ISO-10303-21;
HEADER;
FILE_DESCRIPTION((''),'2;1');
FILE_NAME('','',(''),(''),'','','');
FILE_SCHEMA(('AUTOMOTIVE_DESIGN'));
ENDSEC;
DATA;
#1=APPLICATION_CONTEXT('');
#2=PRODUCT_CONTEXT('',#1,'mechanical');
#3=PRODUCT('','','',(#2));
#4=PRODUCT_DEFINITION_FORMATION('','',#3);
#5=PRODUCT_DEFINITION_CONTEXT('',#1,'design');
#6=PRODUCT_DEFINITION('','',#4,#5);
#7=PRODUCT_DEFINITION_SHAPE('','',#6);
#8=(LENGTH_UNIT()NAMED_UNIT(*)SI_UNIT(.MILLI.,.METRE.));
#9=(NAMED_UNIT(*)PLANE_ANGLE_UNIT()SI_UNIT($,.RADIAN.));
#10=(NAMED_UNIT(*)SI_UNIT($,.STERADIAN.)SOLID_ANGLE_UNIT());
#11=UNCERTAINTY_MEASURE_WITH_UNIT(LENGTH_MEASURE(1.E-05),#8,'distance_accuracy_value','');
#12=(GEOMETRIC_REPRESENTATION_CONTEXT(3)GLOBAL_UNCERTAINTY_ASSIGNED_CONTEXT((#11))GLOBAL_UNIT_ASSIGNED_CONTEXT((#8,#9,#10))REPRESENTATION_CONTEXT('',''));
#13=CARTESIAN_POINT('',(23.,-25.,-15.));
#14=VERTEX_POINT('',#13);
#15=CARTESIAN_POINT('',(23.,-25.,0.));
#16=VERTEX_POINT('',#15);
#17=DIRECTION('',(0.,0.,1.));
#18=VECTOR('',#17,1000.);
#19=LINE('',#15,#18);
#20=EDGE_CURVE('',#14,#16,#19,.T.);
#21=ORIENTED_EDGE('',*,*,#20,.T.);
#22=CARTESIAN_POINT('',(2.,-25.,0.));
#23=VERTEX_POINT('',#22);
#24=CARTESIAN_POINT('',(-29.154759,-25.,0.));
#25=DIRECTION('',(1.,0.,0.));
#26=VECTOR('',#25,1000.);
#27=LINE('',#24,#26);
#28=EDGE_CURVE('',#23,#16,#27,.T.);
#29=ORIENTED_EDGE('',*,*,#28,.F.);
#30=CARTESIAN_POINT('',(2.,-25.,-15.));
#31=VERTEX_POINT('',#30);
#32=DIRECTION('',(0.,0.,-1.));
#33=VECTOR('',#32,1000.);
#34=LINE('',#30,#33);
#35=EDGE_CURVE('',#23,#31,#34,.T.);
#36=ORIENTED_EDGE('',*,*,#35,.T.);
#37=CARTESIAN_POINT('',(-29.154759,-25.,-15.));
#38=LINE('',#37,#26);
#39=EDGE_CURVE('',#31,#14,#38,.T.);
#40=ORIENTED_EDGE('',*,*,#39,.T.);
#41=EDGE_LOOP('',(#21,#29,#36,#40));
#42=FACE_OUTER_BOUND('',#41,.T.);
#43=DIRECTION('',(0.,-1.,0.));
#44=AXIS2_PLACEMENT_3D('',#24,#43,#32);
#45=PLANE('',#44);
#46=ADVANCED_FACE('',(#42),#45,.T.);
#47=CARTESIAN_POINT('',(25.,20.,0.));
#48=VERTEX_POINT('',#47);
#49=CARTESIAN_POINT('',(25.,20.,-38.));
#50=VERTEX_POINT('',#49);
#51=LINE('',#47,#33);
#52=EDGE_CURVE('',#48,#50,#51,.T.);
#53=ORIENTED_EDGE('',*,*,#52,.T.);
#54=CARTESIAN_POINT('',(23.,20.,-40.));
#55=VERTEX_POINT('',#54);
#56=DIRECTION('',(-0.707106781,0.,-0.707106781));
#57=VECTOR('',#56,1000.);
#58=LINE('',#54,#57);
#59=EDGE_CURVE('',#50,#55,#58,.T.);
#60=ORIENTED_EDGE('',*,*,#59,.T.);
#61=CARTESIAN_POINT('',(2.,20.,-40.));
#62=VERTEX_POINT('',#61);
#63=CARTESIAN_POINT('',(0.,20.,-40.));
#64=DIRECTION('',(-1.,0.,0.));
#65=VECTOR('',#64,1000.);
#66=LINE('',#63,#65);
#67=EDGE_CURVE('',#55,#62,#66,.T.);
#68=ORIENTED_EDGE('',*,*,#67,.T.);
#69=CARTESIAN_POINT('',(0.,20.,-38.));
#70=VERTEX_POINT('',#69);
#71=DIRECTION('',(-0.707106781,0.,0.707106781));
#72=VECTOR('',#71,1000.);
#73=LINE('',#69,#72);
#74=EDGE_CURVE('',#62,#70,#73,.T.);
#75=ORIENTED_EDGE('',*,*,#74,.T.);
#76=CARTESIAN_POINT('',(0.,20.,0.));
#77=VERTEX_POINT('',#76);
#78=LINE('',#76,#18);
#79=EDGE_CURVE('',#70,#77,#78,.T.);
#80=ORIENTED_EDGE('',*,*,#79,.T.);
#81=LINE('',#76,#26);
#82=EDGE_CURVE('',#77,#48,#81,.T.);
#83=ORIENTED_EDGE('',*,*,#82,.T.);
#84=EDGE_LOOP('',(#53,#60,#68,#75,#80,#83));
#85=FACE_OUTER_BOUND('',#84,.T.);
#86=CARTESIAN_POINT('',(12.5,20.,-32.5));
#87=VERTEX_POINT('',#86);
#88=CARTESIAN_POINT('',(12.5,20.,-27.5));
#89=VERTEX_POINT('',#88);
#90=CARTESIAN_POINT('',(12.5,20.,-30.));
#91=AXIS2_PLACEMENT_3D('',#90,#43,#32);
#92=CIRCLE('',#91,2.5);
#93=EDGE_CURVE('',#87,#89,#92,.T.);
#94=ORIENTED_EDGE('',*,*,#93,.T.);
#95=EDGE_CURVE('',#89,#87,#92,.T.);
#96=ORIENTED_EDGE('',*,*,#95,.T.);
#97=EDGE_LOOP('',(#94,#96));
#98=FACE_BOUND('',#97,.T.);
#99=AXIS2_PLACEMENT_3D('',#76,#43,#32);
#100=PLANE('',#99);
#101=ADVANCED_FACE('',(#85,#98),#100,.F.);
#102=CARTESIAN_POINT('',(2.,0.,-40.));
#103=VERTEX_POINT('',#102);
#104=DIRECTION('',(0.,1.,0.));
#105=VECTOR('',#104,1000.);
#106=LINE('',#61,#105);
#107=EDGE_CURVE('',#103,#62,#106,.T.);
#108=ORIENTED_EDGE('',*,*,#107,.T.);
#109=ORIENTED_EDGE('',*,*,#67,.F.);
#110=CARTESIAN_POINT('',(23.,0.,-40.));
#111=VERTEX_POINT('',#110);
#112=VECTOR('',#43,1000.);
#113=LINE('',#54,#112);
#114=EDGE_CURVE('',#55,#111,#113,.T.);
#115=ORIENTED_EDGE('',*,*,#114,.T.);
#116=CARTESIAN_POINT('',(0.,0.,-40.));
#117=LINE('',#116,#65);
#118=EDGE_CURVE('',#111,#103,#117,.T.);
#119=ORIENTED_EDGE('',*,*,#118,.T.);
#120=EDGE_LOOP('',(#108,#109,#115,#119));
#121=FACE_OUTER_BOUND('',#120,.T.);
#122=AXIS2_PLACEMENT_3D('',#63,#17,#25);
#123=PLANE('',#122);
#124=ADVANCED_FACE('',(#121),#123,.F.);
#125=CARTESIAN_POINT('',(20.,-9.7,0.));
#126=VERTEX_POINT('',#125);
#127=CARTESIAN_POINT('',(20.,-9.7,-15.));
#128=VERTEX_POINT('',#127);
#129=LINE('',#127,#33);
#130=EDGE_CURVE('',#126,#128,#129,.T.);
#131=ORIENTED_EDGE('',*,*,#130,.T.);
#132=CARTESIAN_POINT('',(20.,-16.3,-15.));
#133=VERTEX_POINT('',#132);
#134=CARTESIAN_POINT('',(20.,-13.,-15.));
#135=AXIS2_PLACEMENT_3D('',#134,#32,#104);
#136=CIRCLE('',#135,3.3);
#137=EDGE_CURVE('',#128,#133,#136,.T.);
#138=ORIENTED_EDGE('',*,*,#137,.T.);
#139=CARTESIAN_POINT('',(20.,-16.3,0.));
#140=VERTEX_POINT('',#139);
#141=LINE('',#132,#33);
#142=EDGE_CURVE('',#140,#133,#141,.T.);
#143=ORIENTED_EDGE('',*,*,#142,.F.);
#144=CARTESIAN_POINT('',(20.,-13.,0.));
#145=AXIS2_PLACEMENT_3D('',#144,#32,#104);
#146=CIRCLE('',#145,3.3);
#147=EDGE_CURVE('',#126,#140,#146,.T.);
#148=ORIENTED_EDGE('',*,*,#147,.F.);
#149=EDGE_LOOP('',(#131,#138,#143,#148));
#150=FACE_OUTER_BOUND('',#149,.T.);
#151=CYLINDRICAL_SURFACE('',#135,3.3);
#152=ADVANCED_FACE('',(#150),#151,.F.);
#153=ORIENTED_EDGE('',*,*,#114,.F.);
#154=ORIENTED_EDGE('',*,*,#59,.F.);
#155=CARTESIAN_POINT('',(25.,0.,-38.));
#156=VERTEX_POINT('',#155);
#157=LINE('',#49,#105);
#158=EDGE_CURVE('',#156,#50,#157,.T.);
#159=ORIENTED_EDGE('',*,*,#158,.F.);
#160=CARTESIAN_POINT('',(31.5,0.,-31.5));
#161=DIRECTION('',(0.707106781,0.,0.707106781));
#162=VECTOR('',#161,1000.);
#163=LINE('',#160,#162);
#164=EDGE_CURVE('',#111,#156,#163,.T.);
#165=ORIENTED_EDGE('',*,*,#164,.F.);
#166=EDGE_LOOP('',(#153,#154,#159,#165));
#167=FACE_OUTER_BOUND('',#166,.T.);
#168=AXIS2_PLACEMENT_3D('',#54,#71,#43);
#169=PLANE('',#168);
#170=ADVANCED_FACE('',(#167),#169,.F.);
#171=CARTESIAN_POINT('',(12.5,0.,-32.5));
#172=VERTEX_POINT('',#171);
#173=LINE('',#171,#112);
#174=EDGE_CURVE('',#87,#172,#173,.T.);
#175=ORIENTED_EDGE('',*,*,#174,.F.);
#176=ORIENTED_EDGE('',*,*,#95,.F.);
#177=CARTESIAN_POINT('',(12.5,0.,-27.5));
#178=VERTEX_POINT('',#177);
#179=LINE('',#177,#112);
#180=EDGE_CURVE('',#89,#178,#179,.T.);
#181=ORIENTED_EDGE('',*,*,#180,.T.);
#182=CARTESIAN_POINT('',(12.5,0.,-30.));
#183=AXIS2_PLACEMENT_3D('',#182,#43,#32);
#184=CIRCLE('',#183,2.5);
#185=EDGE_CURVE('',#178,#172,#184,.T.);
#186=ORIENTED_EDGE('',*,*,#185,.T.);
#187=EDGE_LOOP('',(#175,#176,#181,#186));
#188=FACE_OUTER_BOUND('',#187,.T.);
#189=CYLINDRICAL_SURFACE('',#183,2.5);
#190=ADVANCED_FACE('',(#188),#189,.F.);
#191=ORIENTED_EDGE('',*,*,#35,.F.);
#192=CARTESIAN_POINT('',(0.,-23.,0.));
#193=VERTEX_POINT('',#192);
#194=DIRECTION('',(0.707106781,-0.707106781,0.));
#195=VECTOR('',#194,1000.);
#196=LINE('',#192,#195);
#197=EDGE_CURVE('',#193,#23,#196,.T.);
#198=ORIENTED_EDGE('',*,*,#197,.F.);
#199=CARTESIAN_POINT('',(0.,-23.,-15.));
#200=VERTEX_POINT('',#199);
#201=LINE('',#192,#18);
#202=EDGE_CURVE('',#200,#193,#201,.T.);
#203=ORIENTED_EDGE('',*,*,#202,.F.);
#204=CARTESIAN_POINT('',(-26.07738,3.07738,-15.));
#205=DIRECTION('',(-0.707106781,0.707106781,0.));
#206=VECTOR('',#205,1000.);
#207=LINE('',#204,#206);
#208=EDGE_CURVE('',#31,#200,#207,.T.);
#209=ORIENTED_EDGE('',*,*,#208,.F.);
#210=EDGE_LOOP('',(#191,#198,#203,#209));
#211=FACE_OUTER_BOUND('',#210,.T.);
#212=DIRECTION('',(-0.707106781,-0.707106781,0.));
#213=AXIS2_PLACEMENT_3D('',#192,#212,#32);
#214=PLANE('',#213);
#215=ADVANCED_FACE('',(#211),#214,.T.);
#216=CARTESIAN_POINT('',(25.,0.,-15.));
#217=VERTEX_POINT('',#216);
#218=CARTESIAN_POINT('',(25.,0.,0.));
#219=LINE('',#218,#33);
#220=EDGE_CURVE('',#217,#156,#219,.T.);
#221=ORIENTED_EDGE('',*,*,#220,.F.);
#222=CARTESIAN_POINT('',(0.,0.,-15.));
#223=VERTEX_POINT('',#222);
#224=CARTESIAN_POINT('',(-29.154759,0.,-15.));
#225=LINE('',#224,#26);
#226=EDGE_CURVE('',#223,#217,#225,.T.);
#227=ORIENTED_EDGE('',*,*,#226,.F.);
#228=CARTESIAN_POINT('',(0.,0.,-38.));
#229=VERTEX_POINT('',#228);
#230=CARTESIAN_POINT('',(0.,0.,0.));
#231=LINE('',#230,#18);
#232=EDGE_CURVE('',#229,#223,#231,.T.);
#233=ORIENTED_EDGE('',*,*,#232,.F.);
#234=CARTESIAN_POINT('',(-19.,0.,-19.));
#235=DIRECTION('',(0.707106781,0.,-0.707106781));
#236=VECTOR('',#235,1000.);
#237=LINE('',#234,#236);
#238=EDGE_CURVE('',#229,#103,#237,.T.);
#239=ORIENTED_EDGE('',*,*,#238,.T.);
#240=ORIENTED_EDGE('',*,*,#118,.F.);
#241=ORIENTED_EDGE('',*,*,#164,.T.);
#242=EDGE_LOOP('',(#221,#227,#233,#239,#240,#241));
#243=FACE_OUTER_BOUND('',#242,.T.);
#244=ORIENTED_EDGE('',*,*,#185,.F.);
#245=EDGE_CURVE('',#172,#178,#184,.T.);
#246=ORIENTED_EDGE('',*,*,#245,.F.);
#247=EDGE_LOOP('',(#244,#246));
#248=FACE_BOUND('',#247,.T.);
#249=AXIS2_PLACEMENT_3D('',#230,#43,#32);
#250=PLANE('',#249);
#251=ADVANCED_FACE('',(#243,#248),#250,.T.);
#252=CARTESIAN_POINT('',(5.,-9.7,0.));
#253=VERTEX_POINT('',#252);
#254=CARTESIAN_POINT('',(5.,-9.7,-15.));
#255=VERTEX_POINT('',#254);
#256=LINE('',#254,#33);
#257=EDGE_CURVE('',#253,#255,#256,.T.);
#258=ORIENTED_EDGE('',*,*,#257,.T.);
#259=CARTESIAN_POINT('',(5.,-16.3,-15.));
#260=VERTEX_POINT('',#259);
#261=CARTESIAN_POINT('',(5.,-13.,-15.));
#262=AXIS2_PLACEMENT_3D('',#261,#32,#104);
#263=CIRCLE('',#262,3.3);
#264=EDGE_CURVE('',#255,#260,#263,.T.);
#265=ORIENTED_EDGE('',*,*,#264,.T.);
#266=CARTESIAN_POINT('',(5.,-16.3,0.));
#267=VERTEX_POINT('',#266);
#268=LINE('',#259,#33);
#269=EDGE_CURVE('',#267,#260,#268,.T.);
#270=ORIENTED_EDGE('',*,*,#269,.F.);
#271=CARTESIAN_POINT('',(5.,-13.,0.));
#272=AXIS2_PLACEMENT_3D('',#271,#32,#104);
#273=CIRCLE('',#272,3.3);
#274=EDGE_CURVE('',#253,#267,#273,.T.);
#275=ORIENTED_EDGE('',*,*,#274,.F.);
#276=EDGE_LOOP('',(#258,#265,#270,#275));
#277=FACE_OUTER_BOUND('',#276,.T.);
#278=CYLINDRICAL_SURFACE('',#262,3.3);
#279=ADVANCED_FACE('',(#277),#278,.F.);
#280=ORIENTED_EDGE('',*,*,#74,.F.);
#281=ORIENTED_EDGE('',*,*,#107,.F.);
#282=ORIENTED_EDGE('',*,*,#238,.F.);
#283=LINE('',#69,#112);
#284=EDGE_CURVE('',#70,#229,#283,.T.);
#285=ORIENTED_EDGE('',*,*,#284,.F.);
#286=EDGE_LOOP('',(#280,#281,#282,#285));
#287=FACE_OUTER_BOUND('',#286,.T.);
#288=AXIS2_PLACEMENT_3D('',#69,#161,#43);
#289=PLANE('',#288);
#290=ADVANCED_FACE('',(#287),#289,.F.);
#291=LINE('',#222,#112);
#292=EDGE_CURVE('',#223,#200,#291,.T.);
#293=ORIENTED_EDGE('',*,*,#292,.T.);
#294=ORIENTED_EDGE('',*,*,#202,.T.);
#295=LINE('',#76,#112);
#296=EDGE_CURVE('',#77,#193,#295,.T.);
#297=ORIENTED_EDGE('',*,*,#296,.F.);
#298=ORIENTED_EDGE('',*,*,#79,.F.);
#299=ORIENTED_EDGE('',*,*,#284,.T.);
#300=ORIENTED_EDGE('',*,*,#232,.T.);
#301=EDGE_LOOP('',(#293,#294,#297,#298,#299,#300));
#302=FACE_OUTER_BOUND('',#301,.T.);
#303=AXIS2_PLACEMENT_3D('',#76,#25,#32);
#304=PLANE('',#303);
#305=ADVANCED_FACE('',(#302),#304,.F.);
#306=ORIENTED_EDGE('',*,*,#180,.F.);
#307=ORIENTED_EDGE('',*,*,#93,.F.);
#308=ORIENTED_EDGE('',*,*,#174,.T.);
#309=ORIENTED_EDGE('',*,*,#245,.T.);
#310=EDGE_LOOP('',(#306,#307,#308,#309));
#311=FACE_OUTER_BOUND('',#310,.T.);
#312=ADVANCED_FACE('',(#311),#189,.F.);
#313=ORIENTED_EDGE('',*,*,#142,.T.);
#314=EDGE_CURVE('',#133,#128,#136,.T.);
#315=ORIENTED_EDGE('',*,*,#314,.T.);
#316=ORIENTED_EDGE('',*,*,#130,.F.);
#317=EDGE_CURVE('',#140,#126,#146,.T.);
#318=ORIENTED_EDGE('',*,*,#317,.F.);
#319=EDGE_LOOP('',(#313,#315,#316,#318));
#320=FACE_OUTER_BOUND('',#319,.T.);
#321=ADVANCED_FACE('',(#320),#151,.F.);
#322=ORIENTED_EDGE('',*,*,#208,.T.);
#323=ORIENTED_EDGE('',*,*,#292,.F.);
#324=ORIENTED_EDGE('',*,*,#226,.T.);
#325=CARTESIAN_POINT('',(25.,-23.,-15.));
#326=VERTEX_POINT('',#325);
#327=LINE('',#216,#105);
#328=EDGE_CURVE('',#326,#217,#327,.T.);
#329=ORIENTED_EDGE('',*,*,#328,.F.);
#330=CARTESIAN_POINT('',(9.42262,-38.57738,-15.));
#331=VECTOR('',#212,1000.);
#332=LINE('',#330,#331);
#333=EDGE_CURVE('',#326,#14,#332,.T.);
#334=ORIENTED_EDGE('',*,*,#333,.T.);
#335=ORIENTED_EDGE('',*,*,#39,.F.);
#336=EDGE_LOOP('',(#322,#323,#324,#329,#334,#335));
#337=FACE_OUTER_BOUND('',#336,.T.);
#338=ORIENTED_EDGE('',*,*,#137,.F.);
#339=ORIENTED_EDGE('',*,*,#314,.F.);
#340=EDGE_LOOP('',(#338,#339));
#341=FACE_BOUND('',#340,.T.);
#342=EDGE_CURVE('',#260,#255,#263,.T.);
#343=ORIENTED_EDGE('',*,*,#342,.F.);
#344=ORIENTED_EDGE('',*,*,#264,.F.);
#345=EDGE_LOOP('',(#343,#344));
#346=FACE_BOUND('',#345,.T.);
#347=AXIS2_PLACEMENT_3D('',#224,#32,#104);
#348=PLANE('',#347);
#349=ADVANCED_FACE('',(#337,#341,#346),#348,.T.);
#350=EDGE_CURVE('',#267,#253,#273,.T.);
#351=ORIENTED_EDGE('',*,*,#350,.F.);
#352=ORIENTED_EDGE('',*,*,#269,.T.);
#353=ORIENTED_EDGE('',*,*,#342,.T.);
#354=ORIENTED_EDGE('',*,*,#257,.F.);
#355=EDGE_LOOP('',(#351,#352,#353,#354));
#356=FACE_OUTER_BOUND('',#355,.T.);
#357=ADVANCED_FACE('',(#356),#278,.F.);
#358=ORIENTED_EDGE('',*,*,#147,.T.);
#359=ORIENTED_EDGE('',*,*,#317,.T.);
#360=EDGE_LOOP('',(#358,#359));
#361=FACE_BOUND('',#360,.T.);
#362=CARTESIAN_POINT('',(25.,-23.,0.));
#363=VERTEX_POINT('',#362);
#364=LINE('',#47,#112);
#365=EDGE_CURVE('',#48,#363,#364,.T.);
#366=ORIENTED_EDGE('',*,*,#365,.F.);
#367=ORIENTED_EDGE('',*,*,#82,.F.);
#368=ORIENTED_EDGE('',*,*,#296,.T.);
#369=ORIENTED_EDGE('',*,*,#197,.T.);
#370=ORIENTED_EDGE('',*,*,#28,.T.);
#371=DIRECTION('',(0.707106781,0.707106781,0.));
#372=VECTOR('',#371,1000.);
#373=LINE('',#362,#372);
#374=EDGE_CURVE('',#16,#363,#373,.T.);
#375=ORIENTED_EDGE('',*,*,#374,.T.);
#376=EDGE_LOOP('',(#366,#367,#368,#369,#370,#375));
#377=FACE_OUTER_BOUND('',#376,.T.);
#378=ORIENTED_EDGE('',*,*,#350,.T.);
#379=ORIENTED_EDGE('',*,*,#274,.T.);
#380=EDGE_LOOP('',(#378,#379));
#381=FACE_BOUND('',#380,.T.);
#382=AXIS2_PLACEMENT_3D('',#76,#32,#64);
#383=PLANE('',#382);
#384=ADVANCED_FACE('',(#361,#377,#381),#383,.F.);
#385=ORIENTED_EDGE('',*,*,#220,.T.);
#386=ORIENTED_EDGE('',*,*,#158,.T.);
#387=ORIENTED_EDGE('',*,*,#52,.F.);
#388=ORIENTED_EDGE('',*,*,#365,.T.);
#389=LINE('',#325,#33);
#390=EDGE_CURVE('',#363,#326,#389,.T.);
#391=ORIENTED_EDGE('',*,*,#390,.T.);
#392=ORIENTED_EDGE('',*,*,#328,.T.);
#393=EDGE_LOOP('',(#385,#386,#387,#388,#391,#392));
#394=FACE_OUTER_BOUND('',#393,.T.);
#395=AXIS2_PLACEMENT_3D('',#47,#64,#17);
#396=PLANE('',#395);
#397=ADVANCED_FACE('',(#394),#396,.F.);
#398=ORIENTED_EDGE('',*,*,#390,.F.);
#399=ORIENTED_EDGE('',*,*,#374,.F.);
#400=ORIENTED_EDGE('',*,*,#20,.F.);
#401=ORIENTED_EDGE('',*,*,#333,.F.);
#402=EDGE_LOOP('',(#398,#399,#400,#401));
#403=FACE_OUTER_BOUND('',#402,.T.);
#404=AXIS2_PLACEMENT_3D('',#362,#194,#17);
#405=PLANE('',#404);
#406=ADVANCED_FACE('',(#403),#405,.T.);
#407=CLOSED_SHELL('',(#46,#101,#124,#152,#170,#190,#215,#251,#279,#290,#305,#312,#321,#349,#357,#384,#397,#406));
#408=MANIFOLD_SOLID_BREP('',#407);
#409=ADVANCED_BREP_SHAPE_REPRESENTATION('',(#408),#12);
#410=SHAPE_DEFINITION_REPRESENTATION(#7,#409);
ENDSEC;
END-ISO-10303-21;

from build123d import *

# Parameters (mm, degrees)
SKETCH_1_W           = 25
SKETCH_1_H           = 40
EXTRUDE_1_DEPTH      = 20
CHAMFER_1_SIZE       = 2
HOLE_WIZARD_M6_1_D   = 5
SKETCH_6_W           = 15
SKETCH_6_H           = 25
EXTRUDE_2_DEPTH      = 25
HOLE_WIZARD_M6_1_2_D = 6.6
CHAMFER_2_SIZE       = 2


with BuildPart() as part:
    # 草图1 → 凸台-拉伸1 (new body)
    with BuildSketch(Plane(origin=(0, 0, 0), x_dir=(1, 0, 0), z_dir=(0, 1, 0))):
        with Locations((12.5, 20)):
            Rectangle(SKETCH_1_W, SKETCH_1_H)
    extrude(amount=EXTRUDE_1_DEPTH)

    # 倒角1
    chamfer_1_edges = [part.edges().sort_by_distance(p)[0] for p in [
        (0, 10, -40),
        (25, 10, -40),
    ]]
    chamfer(chamfer_1_edges, length=CHAMFER_1_SIZE)

    # Hole Wizard M6 _1 (through all)
    with Locations(Plane(origin=(0, 0, 0), x_dir=(-1, 0, 0), z_dir=(0, -1, 0))):
        with Locations((-12.5, 30)):
            Hole(HOLE_WIZARD_M6_1_D / 2)

    # 草图6 → 凸台-拉伸2 (add)
    with BuildSketch(Plane(origin=(25, 0, 0), x_dir=(0, 0, -1), z_dir=(1, 0, 0))):
        with Locations((7.5, -12.5)):
            Rectangle(SKETCH_6_W, SKETCH_6_H)
    extrude(amount=-EXTRUDE_2_DEPTH)

    # Hole Wizard M6 _1 2 (through all)
    with Locations(Plane(origin=(0, 0, -15), x_dir=(-1, 0, 0), z_dir=(0, 0, -1))):
        with Locations((-20, -13), (-5, -13)):
            Hole(HOLE_WIZARD_M6_1_2_D / 2)

    # 倒角2
    chamfer_2_edges = [part.edges().sort_by_distance(p)[0] for p in [
        (25, -25, -7.5),
        (0, -25, -7.5),
    ]]
    chamfer(chamfer_2_edges, length=CHAMFER_2_SIZE)


solid = part.part
